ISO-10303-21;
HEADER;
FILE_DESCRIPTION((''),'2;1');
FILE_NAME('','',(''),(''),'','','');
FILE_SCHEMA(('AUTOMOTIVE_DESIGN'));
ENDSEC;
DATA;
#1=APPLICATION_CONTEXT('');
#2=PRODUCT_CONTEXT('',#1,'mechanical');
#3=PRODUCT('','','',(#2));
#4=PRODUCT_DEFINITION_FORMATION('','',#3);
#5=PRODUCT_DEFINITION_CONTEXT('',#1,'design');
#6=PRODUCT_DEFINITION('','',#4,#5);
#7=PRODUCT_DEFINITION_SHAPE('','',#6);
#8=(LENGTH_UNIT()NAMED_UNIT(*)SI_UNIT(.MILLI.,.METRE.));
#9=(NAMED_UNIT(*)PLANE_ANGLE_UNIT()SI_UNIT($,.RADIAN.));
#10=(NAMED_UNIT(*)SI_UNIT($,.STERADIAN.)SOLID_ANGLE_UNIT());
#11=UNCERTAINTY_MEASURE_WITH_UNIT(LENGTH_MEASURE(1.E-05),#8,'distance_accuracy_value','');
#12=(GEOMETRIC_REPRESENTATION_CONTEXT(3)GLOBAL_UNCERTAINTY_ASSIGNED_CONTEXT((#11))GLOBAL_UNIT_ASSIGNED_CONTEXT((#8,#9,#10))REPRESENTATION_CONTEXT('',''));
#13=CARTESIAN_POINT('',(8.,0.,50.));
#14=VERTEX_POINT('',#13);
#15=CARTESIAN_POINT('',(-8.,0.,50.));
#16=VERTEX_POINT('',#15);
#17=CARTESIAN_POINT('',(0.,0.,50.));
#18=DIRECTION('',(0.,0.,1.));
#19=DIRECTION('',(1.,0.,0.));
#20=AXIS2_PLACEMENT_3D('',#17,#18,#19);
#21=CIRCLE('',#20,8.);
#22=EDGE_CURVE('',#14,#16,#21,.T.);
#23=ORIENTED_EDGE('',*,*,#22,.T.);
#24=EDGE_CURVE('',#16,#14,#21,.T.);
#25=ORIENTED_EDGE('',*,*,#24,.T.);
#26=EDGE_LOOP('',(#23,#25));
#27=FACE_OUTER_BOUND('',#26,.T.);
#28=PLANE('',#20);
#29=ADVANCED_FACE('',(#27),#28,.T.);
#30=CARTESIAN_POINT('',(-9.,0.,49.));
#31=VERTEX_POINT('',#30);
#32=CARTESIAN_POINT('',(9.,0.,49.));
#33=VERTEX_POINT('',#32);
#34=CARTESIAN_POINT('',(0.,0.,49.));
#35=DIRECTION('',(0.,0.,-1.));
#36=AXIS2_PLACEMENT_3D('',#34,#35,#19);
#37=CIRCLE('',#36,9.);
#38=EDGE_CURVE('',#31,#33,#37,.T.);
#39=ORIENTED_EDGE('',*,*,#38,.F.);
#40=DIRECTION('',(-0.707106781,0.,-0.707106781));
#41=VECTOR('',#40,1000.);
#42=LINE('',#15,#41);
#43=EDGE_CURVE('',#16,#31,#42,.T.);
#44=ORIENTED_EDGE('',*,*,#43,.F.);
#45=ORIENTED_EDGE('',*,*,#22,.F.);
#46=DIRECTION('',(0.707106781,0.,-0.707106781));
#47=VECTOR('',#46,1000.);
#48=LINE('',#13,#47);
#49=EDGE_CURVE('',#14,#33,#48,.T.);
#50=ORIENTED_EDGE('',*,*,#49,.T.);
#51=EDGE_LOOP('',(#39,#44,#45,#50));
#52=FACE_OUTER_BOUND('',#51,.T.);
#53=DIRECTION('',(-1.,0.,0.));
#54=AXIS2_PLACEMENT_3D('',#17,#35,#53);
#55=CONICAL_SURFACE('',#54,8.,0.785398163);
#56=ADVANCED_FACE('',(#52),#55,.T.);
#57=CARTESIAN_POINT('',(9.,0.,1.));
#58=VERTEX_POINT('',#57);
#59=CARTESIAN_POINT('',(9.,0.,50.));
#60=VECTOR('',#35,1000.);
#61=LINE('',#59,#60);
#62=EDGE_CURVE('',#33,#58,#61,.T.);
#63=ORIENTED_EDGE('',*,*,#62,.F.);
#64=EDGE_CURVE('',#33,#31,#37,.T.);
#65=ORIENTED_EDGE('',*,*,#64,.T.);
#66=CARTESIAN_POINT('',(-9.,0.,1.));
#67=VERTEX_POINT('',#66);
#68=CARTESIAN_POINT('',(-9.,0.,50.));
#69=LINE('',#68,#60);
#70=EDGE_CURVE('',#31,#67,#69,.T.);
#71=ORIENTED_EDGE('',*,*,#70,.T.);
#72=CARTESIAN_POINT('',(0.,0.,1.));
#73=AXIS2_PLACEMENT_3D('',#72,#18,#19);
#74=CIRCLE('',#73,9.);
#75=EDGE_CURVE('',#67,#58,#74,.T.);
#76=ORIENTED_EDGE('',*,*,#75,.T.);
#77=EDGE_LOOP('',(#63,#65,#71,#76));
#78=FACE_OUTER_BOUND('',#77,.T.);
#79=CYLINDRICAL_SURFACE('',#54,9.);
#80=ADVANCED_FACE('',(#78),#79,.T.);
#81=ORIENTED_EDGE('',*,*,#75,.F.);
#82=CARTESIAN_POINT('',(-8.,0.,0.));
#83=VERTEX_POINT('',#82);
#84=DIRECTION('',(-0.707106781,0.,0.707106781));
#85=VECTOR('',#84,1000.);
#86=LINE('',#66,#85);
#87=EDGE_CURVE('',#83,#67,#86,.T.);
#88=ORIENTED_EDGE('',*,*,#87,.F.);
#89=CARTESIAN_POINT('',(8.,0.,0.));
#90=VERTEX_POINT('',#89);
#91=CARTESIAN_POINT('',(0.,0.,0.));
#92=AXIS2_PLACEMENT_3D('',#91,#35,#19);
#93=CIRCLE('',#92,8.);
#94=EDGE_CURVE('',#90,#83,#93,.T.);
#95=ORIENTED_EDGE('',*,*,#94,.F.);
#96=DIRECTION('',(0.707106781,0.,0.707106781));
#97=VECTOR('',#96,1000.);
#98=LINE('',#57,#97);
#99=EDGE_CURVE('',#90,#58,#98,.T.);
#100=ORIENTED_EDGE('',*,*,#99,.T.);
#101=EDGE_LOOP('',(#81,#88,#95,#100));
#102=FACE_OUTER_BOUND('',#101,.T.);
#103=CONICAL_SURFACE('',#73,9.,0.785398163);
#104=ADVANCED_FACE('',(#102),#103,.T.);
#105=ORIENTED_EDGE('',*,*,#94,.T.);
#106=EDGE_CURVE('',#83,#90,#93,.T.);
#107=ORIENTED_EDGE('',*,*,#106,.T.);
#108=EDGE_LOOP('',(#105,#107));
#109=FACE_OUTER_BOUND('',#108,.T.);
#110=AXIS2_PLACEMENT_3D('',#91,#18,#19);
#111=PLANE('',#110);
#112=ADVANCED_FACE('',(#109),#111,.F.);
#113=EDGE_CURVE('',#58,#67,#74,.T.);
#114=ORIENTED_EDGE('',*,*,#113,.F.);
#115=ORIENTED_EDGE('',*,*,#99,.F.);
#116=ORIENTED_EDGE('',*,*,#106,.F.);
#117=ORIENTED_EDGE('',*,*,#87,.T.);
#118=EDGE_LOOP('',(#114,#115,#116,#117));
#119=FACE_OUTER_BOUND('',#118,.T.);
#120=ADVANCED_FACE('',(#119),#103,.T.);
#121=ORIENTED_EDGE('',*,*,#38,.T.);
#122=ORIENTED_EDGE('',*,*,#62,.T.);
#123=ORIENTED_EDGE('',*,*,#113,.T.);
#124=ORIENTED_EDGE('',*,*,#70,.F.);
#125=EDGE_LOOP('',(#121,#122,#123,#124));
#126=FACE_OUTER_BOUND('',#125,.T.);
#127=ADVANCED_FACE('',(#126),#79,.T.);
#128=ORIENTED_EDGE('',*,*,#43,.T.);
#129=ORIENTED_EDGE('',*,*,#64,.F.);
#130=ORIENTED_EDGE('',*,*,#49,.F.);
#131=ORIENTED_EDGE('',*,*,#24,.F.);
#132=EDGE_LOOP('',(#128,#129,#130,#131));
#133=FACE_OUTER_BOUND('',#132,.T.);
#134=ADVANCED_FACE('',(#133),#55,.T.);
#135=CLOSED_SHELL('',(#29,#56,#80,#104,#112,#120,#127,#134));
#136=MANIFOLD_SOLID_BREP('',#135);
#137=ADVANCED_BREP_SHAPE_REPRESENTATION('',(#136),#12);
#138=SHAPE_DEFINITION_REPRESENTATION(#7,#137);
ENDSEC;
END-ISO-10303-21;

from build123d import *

# Parameters (mm, degrees)
SKETCH1_R           = 9
BOSS_EXTRUDE1_DEPTH = 50
CHAMFER1_SIZE       = 1


with BuildPart() as part:
    # Sketch1 → Boss-Extrude1 (new body)
    with BuildSketch(Plane.XY):
        Circle(SKETCH1_R)
    extrude(amount=BOSS_EXTRUDE1_DEPTH)

    # Chamfer1
    chamfer1_edges = [part.edges().sort_by_distance(p)[0] for p in [
        (-9, 0, 0),
        (-9, 0, 50),
    ]]
    chamfer(chamfer1_edges, length=CHAMFER1_SIZE)


solid = part.part
